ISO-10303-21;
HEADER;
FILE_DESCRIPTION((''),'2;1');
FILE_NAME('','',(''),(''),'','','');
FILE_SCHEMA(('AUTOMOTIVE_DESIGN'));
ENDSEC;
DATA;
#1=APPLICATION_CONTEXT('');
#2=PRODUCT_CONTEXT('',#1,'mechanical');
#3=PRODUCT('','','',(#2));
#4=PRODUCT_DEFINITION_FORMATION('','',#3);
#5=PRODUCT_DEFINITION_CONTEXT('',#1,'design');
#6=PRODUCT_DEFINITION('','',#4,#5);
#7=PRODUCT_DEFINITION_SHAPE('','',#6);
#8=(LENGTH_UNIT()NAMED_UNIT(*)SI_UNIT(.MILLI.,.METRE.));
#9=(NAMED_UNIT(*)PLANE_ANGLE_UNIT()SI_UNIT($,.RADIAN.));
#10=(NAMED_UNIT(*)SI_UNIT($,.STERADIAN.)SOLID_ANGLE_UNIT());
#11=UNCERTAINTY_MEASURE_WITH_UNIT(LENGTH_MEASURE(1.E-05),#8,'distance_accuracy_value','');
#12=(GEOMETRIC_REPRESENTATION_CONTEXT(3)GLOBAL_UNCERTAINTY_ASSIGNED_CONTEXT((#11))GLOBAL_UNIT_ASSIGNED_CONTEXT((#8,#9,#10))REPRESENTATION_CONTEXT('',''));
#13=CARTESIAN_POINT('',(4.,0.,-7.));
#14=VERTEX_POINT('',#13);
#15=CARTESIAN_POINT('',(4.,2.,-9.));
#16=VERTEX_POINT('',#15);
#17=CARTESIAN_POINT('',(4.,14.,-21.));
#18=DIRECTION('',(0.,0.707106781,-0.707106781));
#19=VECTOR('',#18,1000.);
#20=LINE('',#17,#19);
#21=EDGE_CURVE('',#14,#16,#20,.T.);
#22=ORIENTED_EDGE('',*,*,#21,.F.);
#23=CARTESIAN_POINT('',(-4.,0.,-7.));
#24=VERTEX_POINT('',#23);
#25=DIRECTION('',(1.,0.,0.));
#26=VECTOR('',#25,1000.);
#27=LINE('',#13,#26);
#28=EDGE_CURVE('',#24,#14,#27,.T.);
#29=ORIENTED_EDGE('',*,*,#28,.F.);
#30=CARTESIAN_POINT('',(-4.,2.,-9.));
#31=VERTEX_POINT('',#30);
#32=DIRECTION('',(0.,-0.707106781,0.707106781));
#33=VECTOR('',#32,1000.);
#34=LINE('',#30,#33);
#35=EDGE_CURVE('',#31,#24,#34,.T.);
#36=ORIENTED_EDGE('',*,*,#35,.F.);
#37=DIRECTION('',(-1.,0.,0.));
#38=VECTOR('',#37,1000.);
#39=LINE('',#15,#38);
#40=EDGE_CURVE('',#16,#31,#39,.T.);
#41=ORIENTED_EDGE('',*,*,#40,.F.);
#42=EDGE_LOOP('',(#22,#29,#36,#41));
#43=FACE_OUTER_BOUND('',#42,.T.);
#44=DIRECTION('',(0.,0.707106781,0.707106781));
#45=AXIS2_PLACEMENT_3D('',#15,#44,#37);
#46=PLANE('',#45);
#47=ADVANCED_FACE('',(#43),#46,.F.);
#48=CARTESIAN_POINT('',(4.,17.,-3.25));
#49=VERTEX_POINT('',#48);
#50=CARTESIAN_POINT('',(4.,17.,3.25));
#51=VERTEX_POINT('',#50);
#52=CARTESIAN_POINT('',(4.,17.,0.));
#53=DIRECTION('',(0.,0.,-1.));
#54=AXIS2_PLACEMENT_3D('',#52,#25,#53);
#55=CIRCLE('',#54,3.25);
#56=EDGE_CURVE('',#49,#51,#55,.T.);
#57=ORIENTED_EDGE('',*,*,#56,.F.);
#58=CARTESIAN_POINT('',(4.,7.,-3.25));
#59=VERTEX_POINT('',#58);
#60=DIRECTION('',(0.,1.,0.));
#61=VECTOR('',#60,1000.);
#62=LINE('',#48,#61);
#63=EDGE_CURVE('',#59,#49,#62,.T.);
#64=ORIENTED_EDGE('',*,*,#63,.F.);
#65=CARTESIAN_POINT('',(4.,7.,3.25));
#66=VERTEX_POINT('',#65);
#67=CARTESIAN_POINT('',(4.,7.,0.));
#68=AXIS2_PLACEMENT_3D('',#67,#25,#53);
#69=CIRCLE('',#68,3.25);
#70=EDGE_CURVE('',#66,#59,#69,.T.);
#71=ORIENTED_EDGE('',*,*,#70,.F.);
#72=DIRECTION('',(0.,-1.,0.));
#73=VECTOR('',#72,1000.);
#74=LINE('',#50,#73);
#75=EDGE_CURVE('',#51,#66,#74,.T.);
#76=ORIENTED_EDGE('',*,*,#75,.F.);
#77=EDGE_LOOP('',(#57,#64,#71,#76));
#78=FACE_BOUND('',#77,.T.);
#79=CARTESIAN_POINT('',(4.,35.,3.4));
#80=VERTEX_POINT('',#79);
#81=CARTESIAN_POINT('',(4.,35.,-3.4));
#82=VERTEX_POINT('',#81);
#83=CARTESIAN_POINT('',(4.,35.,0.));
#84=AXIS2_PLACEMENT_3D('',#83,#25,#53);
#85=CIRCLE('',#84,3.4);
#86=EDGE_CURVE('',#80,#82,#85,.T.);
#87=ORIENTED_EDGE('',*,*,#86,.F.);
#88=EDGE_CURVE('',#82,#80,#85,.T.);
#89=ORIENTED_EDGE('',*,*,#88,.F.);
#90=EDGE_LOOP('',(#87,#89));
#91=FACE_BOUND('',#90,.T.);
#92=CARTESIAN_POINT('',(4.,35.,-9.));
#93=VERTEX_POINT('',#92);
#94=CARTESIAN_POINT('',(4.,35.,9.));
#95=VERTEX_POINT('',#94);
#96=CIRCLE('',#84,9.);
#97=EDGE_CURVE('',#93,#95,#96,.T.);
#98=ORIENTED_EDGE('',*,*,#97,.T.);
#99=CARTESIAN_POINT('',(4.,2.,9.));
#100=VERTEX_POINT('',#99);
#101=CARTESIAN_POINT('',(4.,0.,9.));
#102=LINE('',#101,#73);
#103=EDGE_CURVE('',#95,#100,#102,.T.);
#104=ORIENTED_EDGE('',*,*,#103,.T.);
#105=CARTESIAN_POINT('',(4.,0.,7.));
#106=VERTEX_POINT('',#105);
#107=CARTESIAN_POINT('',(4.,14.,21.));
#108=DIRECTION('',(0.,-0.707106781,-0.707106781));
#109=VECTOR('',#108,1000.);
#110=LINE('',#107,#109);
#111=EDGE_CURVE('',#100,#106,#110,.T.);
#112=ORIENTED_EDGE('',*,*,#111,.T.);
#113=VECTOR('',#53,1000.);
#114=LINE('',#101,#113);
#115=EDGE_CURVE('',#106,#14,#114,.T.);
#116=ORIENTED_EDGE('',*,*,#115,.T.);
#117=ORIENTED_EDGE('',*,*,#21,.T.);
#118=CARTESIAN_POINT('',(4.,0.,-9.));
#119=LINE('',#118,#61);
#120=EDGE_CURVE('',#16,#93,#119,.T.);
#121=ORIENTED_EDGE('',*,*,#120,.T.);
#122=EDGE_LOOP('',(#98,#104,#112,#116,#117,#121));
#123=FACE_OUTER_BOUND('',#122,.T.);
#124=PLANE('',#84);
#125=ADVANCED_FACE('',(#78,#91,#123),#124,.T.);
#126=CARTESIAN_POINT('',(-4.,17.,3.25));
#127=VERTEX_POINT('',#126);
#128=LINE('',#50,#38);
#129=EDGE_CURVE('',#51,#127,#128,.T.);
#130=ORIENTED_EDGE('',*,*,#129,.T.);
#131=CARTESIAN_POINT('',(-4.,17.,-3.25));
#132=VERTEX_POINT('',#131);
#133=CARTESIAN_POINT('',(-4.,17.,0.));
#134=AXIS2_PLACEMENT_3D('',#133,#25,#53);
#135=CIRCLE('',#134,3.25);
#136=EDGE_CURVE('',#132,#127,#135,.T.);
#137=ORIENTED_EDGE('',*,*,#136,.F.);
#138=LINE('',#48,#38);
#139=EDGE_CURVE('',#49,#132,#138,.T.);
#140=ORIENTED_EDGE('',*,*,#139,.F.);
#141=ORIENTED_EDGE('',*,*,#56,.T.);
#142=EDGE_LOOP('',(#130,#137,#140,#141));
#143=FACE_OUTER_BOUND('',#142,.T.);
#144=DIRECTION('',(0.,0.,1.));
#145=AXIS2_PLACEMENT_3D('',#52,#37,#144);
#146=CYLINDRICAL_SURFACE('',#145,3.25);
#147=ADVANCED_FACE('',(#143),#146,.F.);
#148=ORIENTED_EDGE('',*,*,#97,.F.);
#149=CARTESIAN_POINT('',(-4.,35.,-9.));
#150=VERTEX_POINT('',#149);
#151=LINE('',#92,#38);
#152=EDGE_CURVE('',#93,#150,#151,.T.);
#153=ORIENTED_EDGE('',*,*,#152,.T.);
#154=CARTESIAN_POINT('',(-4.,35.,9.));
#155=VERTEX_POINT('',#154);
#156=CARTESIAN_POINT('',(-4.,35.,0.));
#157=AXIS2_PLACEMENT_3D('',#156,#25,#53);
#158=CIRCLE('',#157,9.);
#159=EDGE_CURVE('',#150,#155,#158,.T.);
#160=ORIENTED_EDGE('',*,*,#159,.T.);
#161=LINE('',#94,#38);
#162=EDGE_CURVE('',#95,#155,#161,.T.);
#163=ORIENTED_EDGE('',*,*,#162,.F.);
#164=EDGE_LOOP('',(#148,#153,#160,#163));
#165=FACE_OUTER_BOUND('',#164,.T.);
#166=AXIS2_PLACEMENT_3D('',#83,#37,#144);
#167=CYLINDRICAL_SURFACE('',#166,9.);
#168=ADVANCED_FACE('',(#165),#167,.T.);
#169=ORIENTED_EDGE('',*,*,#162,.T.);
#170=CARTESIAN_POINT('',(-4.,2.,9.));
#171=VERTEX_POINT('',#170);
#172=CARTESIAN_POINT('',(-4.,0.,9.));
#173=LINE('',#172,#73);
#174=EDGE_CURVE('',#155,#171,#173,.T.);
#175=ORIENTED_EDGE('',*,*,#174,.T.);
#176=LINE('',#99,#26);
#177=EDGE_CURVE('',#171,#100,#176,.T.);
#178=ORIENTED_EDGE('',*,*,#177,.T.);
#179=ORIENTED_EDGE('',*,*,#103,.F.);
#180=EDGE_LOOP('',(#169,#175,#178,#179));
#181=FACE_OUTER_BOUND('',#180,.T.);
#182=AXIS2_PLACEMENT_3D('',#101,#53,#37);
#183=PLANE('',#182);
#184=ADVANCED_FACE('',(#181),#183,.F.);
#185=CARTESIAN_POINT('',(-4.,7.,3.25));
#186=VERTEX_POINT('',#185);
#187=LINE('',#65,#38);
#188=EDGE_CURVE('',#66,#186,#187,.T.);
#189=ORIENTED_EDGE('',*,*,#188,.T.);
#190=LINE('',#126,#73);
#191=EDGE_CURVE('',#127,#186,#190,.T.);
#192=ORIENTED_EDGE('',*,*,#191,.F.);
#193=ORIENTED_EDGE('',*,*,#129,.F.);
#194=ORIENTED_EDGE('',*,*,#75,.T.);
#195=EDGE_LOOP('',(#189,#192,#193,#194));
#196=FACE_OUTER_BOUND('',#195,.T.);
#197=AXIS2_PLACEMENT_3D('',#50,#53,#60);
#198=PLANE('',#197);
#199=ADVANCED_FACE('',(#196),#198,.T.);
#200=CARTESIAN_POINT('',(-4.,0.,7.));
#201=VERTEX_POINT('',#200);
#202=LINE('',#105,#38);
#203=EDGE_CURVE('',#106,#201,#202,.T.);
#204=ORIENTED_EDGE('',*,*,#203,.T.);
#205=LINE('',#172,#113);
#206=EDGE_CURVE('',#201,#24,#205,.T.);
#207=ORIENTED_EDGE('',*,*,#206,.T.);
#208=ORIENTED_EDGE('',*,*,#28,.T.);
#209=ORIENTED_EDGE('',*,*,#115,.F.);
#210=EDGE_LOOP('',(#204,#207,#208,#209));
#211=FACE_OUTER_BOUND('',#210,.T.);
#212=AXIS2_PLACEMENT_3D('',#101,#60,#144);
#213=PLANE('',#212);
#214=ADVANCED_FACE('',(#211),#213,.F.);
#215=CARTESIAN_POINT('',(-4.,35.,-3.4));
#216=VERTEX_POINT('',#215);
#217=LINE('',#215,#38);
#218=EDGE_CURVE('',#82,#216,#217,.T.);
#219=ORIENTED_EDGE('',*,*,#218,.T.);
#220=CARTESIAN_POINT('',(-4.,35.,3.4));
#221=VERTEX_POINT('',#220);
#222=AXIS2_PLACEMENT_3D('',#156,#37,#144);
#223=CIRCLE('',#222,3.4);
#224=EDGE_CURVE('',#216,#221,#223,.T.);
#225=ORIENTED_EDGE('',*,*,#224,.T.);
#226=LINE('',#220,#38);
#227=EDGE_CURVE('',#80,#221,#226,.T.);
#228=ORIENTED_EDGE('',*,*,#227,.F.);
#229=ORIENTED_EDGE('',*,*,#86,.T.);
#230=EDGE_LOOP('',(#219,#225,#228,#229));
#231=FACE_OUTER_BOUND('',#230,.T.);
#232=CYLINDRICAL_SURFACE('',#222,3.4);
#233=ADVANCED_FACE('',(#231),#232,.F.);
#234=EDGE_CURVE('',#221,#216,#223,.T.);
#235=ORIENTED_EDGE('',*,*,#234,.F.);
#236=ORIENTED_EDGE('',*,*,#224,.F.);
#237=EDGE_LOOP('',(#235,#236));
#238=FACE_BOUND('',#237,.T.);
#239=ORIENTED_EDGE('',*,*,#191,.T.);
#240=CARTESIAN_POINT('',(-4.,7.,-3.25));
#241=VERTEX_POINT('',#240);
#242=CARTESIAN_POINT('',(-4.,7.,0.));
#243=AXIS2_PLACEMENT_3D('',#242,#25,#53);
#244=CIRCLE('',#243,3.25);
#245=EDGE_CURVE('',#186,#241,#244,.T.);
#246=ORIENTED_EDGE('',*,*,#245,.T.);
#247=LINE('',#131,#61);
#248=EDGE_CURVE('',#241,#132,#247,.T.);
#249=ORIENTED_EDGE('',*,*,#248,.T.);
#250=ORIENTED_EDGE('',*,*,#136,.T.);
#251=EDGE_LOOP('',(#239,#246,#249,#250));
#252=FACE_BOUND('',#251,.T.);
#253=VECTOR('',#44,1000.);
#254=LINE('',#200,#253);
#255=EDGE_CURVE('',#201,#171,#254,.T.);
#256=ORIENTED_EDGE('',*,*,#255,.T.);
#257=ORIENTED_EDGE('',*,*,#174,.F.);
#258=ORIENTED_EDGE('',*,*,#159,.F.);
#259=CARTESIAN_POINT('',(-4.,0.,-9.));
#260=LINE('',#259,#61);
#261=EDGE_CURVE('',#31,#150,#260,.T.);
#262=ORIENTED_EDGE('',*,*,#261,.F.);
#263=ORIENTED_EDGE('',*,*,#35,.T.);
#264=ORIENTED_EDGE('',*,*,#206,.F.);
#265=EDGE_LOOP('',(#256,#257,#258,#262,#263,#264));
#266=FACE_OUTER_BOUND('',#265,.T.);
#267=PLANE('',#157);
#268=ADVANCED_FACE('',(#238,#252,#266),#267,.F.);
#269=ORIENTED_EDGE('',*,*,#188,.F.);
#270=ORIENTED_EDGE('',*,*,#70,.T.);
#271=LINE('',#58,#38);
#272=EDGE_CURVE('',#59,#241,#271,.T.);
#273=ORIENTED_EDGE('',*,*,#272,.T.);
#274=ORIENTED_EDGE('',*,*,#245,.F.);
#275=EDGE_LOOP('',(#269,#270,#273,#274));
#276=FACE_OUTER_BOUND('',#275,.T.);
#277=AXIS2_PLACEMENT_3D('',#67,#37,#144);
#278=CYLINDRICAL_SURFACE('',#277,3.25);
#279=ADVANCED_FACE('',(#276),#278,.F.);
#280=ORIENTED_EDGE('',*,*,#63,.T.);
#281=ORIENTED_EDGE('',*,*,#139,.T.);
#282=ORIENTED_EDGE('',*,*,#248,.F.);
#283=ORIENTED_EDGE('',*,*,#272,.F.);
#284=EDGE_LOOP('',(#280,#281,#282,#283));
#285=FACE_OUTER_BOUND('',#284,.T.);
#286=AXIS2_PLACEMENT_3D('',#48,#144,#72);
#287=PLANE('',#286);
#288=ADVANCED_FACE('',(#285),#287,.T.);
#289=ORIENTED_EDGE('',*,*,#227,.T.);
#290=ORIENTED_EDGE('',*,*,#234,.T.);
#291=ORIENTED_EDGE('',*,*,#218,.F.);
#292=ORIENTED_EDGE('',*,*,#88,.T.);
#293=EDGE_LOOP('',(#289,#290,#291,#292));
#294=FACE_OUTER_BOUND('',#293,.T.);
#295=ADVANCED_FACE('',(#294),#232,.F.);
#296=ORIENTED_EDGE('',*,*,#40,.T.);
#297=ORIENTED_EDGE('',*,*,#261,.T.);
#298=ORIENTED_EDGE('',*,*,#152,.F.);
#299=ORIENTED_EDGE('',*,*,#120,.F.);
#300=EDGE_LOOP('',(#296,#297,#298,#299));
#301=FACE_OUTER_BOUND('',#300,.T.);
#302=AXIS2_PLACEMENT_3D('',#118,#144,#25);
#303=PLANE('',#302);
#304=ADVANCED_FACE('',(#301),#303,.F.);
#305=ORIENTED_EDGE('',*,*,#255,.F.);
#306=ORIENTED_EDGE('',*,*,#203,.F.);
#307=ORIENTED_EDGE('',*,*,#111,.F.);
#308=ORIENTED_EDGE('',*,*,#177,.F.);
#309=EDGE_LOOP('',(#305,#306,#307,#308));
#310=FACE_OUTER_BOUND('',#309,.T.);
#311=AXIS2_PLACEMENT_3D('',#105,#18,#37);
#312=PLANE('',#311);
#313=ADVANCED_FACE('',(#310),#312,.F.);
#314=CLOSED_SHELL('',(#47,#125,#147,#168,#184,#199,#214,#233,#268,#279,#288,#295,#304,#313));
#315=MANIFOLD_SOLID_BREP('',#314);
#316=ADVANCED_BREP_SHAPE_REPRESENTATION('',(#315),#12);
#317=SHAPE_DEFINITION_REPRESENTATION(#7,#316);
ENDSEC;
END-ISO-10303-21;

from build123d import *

# Parameters (mm, degrees)
BOSS_EXTRUDE1_DEPTH   = 4
M8_TAPPED_HOLE1_D     = 6.8
M8_TAPPED_HOLE1_DEPTH = 22.25
M8_TAPPED_HOLE1_TIP   = 2.042926105
CHAMFER1_SIZE         = 2


with BuildPart() as part:
    # Sketch1 → Boss-Extrude1 (new, symmetric)
    with BuildSketch(Plane(origin=(0, 0, 0), x_dir=(0, 0, -1), z_dir=(1, 0, 0))):
        with BuildLine():
            Line((-9, 0), (9, 0))
            Line((9, 0), (9, 35))
            ThreePointArc((9, 35), (0, 44), (-9, 35))
            Line((-9, 35), (-9, 0))
        make_face()
        with BuildLine():
            Line((3.25, 17), (3.25, 7))
            ThreePointArc((3.25, 7), (0, 3.75), (-3.25, 7))
            Line((-3.25, 7), (-3.25, 17))
            ThreePointArc((-3.25, 17), (0, 20.25), (3.25, 17))
        make_face(mode=Mode.SUBTRACT)
    extrude(amount=BOSS_EXTRUDE1_DEPTH, both=True)

    # M8 Tapped Hole1
    with Locations(Plane.ZY.offset(4)):
        with Locations((0, 35)):
            Hole(M8_TAPPED_HOLE1_D / 2, depth=M8_TAPPED_HOLE1_DEPTH)
            with Locations((0, 0, -(M8_TAPPED_HOLE1_DEPTH + M8_TAPPED_HOLE1_TIP / 2))):  # 118° drill point
                Cone(0, M8_TAPPED_HOLE1_D / 2, M8_TAPPED_HOLE1_TIP, mode=Mode.SUBTRACT)

    # Chamfer1
    chamfer1_edges = [part.edges().sort_by_distance(p)[0] for p in [
        (0, 0, -9),
        (0, 0, 9),
    ]]
    chamfer(chamfer1_edges, length=CHAMFER1_SIZE)


solid = part.part
